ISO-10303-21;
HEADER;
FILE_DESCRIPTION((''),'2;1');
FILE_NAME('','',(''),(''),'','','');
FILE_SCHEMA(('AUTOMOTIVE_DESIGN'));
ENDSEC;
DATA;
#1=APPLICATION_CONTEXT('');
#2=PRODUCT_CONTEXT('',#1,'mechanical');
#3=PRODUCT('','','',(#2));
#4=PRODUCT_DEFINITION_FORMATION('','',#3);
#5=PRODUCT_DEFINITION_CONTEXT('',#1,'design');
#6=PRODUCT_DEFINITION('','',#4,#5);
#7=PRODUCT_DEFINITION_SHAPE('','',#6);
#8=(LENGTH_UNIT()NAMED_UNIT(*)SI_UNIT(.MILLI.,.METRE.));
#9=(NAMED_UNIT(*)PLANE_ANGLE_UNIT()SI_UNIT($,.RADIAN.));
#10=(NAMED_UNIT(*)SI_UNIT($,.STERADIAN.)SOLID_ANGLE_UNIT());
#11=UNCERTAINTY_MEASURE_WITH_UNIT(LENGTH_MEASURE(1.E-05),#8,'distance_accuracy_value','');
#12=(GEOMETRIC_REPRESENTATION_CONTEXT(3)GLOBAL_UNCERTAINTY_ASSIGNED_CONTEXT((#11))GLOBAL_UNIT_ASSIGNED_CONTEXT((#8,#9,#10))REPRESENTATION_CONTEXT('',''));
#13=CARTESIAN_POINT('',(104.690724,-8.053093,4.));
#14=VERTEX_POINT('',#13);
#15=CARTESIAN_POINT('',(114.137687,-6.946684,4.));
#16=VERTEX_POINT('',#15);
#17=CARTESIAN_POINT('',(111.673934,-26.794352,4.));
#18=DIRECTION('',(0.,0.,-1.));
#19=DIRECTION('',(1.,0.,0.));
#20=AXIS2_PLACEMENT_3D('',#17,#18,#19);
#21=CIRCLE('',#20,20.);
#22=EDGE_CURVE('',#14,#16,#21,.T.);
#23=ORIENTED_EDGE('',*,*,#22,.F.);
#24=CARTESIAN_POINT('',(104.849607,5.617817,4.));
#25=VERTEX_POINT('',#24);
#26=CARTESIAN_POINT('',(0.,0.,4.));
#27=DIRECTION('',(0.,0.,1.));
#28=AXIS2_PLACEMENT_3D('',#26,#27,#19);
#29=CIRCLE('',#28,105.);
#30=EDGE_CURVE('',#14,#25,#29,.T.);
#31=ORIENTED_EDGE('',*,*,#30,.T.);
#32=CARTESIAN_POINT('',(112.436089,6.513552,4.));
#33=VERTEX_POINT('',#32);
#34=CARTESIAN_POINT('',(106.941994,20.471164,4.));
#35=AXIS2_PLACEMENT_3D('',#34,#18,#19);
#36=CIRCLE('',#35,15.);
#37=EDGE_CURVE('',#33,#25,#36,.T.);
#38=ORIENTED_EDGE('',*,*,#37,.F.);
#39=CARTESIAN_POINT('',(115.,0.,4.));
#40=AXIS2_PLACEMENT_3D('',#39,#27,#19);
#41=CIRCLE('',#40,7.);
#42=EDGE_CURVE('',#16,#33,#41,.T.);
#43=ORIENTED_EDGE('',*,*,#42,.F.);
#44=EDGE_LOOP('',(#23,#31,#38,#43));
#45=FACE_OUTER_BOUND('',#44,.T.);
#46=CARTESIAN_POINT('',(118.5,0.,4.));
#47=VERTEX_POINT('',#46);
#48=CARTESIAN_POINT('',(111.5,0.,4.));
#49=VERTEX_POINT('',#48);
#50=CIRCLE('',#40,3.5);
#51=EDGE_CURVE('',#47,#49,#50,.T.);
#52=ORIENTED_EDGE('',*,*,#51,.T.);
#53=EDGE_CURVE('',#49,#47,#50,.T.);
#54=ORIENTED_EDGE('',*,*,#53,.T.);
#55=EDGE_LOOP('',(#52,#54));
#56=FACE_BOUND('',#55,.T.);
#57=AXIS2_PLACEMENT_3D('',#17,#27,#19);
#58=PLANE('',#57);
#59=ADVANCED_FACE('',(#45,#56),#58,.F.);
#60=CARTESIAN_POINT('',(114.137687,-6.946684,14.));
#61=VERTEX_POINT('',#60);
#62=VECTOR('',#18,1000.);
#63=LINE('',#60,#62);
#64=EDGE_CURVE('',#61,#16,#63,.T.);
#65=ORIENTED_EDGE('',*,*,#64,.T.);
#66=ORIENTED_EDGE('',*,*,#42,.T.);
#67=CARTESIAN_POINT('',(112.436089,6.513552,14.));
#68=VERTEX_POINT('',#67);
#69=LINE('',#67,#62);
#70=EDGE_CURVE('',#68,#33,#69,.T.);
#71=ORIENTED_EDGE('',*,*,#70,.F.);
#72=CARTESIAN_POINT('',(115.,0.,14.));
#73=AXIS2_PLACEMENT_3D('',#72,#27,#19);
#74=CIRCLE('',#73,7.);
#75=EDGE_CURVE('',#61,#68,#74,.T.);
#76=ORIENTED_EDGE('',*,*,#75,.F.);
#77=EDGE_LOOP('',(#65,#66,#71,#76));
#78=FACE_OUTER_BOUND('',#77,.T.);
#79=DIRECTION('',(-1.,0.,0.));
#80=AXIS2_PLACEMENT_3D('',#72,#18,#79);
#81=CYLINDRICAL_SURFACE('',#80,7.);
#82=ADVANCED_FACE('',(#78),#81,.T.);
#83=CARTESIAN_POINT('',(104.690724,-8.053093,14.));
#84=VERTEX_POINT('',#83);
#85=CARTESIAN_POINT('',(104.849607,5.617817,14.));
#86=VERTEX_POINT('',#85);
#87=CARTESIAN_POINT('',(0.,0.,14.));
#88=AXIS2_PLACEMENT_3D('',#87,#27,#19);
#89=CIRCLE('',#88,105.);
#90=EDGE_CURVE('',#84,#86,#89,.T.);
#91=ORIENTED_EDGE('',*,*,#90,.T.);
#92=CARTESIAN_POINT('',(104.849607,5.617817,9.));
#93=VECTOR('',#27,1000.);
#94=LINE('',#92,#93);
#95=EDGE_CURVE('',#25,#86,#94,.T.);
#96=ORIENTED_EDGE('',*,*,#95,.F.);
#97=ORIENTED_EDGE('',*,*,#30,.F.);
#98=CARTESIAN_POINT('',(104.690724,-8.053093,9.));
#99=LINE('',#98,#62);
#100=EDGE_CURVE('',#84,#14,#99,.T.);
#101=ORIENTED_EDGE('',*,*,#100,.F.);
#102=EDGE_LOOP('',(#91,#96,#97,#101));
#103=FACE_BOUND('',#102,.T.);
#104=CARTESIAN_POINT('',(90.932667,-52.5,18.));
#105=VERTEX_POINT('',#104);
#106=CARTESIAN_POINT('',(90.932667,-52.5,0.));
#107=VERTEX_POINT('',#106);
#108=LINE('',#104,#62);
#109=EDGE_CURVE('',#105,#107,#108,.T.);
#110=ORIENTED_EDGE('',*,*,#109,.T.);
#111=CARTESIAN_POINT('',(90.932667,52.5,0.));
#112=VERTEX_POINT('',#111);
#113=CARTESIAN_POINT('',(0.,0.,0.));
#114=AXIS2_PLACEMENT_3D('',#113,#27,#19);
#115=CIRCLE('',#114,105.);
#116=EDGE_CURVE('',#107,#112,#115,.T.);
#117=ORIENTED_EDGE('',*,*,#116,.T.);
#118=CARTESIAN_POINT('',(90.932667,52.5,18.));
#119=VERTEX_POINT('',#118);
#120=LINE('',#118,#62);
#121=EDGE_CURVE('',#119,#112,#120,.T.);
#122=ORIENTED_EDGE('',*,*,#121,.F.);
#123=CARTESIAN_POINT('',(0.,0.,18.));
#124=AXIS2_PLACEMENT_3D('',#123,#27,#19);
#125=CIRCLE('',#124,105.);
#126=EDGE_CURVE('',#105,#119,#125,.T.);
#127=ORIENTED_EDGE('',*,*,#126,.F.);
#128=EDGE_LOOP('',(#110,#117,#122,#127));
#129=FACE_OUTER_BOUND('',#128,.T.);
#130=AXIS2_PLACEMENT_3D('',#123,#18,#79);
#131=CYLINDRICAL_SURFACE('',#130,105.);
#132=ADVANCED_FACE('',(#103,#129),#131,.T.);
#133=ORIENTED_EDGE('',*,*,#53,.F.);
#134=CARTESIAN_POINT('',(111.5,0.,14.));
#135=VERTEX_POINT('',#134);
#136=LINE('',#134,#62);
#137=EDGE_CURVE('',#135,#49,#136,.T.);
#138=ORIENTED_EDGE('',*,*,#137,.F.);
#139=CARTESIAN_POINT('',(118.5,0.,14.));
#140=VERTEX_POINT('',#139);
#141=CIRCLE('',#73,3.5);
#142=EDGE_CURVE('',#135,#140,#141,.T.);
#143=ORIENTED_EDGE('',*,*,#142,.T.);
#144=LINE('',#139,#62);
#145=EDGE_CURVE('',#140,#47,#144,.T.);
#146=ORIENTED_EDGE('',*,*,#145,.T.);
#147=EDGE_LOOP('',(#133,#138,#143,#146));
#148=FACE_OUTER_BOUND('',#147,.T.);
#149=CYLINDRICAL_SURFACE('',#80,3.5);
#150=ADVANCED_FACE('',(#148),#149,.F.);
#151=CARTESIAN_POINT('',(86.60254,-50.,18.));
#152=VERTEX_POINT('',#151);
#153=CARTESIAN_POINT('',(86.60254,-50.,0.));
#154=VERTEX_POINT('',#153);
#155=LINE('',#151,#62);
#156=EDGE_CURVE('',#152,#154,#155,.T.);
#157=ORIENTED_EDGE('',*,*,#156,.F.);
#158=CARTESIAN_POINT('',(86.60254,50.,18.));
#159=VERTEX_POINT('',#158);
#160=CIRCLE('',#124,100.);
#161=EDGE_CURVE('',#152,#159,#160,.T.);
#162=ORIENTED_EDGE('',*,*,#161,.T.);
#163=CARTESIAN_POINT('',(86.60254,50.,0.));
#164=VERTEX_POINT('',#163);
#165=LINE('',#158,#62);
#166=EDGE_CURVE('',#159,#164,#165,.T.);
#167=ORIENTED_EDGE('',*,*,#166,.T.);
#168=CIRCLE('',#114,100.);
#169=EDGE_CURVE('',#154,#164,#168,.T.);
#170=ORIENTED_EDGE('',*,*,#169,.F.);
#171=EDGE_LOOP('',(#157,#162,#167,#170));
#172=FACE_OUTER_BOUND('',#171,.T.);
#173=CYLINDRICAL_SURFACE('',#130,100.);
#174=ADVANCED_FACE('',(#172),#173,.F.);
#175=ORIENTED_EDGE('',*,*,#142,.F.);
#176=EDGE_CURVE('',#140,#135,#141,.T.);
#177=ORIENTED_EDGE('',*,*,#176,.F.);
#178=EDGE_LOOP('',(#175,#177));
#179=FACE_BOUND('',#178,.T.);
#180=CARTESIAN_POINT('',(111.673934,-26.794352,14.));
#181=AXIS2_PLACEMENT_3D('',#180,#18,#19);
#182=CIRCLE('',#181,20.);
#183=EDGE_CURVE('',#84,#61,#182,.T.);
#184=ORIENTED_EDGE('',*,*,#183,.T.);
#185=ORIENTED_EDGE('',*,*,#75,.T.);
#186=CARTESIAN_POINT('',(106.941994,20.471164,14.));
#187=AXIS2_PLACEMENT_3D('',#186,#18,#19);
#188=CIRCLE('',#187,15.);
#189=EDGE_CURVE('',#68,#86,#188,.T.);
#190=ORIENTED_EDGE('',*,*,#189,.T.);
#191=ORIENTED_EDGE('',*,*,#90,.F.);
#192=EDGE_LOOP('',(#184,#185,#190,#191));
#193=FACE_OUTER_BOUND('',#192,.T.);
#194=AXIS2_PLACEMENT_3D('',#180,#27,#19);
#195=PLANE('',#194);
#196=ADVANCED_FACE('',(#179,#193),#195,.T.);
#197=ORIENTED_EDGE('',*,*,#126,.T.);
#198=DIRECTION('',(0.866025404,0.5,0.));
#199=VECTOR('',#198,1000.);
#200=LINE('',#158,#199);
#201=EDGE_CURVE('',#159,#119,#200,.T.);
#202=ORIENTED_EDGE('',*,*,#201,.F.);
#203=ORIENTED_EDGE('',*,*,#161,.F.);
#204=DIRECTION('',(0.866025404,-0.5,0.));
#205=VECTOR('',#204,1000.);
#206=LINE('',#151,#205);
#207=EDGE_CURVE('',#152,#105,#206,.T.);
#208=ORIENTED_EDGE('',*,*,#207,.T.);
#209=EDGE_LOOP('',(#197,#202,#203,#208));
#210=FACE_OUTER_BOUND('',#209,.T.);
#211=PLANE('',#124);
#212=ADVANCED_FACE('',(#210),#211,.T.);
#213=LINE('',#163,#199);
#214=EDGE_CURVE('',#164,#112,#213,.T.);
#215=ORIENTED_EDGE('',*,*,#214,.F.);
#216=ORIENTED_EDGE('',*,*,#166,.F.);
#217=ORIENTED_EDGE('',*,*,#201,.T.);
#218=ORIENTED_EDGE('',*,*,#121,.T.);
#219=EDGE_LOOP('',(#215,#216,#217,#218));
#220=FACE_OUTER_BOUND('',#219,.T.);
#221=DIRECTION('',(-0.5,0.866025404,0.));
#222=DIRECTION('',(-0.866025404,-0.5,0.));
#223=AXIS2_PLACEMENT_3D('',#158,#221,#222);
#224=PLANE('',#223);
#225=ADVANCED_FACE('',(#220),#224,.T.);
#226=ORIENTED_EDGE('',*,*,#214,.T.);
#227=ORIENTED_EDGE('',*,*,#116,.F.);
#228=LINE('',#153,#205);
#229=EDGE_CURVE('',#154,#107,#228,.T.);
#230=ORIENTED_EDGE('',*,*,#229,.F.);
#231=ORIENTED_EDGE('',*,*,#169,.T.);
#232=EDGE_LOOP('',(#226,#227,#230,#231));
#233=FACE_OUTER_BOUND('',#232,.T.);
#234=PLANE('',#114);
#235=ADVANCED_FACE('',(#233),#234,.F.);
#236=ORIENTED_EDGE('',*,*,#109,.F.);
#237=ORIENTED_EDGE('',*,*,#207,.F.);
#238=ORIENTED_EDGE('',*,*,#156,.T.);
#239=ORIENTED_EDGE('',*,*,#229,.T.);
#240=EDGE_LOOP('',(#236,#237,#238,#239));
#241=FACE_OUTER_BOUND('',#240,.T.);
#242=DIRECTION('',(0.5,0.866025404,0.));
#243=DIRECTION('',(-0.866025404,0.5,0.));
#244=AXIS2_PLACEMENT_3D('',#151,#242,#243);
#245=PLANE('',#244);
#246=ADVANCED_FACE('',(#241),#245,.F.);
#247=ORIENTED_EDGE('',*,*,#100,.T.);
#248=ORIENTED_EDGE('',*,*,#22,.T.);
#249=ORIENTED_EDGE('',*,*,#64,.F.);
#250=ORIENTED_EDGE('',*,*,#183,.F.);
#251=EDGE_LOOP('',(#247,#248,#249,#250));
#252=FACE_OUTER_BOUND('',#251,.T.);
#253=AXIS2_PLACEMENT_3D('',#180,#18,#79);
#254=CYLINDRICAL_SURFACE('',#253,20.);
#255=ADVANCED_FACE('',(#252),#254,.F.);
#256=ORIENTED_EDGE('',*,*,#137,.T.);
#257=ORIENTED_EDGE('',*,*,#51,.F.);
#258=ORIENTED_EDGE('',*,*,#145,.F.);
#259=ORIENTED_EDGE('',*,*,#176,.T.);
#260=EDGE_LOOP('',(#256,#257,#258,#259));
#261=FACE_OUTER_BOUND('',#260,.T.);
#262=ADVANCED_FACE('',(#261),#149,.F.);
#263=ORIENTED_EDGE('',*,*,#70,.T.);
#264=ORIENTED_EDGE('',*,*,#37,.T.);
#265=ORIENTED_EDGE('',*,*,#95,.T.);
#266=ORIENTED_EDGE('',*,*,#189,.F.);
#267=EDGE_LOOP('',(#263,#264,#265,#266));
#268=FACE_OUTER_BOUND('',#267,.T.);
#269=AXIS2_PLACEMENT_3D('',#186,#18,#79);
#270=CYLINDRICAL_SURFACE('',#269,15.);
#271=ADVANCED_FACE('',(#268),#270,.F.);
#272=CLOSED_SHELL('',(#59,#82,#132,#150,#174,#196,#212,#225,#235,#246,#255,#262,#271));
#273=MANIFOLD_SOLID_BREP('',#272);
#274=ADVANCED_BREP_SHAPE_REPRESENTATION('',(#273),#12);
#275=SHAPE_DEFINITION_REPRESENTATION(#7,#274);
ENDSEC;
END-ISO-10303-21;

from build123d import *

# Parameters (mm, degrees)
EXTRUDE_1_DEPTH = 18
SKETCH_8_R      = 3.5
EXTRUDE_5_DEPTH = 5


with BuildPart() as part:
    # 草图1 → 凸台-拉伸1 (new body)
    with BuildSketch(Plane.XY):
        with BuildLine():
            Line((86.602540378, 50), (90.932667397, 52.5))
            ThreePointArc((90.932667397, 52.5), (105, 0), (90.932667397, -52.5))
            Line((90.932667397, -52.5), (86.602540378, -50))
            ThreePointArc((86.602540378, -50), (100, 0), (86.602540378, 50))
        make_face()
    extrude(amount=EXTRUDE_1_DEPTH)

    # 草图8 → 凸台-拉伸5 (add, symmetric)
    with BuildSketch(Plane.XY.offset(9)):
        with BuildLine():
            Line((103.468607759, 5.878851187), (102.726389869, -8.907444453))
            ThreePointArc((102.726389869, -8.907444453), (108.287042552, -7.083213633), (114.137686614, -6.946683786))
            ThreePointArc((114.137686614, -6.946683786), (121.944727548, 0.877928973), (112.436089109, 6.513552099))
            ThreePointArc((112.436089109, 6.513552099), (108.00101592, 5.508594665), (103.468607759, 5.878851187))
        make_face()
        with Locations((115, 0)):
            Circle(SKETCH_8_R, mode=Mode.SUBTRACT)
    extrude(amount=EXTRUDE_5_DEPTH, both=True)


solid = part.part
